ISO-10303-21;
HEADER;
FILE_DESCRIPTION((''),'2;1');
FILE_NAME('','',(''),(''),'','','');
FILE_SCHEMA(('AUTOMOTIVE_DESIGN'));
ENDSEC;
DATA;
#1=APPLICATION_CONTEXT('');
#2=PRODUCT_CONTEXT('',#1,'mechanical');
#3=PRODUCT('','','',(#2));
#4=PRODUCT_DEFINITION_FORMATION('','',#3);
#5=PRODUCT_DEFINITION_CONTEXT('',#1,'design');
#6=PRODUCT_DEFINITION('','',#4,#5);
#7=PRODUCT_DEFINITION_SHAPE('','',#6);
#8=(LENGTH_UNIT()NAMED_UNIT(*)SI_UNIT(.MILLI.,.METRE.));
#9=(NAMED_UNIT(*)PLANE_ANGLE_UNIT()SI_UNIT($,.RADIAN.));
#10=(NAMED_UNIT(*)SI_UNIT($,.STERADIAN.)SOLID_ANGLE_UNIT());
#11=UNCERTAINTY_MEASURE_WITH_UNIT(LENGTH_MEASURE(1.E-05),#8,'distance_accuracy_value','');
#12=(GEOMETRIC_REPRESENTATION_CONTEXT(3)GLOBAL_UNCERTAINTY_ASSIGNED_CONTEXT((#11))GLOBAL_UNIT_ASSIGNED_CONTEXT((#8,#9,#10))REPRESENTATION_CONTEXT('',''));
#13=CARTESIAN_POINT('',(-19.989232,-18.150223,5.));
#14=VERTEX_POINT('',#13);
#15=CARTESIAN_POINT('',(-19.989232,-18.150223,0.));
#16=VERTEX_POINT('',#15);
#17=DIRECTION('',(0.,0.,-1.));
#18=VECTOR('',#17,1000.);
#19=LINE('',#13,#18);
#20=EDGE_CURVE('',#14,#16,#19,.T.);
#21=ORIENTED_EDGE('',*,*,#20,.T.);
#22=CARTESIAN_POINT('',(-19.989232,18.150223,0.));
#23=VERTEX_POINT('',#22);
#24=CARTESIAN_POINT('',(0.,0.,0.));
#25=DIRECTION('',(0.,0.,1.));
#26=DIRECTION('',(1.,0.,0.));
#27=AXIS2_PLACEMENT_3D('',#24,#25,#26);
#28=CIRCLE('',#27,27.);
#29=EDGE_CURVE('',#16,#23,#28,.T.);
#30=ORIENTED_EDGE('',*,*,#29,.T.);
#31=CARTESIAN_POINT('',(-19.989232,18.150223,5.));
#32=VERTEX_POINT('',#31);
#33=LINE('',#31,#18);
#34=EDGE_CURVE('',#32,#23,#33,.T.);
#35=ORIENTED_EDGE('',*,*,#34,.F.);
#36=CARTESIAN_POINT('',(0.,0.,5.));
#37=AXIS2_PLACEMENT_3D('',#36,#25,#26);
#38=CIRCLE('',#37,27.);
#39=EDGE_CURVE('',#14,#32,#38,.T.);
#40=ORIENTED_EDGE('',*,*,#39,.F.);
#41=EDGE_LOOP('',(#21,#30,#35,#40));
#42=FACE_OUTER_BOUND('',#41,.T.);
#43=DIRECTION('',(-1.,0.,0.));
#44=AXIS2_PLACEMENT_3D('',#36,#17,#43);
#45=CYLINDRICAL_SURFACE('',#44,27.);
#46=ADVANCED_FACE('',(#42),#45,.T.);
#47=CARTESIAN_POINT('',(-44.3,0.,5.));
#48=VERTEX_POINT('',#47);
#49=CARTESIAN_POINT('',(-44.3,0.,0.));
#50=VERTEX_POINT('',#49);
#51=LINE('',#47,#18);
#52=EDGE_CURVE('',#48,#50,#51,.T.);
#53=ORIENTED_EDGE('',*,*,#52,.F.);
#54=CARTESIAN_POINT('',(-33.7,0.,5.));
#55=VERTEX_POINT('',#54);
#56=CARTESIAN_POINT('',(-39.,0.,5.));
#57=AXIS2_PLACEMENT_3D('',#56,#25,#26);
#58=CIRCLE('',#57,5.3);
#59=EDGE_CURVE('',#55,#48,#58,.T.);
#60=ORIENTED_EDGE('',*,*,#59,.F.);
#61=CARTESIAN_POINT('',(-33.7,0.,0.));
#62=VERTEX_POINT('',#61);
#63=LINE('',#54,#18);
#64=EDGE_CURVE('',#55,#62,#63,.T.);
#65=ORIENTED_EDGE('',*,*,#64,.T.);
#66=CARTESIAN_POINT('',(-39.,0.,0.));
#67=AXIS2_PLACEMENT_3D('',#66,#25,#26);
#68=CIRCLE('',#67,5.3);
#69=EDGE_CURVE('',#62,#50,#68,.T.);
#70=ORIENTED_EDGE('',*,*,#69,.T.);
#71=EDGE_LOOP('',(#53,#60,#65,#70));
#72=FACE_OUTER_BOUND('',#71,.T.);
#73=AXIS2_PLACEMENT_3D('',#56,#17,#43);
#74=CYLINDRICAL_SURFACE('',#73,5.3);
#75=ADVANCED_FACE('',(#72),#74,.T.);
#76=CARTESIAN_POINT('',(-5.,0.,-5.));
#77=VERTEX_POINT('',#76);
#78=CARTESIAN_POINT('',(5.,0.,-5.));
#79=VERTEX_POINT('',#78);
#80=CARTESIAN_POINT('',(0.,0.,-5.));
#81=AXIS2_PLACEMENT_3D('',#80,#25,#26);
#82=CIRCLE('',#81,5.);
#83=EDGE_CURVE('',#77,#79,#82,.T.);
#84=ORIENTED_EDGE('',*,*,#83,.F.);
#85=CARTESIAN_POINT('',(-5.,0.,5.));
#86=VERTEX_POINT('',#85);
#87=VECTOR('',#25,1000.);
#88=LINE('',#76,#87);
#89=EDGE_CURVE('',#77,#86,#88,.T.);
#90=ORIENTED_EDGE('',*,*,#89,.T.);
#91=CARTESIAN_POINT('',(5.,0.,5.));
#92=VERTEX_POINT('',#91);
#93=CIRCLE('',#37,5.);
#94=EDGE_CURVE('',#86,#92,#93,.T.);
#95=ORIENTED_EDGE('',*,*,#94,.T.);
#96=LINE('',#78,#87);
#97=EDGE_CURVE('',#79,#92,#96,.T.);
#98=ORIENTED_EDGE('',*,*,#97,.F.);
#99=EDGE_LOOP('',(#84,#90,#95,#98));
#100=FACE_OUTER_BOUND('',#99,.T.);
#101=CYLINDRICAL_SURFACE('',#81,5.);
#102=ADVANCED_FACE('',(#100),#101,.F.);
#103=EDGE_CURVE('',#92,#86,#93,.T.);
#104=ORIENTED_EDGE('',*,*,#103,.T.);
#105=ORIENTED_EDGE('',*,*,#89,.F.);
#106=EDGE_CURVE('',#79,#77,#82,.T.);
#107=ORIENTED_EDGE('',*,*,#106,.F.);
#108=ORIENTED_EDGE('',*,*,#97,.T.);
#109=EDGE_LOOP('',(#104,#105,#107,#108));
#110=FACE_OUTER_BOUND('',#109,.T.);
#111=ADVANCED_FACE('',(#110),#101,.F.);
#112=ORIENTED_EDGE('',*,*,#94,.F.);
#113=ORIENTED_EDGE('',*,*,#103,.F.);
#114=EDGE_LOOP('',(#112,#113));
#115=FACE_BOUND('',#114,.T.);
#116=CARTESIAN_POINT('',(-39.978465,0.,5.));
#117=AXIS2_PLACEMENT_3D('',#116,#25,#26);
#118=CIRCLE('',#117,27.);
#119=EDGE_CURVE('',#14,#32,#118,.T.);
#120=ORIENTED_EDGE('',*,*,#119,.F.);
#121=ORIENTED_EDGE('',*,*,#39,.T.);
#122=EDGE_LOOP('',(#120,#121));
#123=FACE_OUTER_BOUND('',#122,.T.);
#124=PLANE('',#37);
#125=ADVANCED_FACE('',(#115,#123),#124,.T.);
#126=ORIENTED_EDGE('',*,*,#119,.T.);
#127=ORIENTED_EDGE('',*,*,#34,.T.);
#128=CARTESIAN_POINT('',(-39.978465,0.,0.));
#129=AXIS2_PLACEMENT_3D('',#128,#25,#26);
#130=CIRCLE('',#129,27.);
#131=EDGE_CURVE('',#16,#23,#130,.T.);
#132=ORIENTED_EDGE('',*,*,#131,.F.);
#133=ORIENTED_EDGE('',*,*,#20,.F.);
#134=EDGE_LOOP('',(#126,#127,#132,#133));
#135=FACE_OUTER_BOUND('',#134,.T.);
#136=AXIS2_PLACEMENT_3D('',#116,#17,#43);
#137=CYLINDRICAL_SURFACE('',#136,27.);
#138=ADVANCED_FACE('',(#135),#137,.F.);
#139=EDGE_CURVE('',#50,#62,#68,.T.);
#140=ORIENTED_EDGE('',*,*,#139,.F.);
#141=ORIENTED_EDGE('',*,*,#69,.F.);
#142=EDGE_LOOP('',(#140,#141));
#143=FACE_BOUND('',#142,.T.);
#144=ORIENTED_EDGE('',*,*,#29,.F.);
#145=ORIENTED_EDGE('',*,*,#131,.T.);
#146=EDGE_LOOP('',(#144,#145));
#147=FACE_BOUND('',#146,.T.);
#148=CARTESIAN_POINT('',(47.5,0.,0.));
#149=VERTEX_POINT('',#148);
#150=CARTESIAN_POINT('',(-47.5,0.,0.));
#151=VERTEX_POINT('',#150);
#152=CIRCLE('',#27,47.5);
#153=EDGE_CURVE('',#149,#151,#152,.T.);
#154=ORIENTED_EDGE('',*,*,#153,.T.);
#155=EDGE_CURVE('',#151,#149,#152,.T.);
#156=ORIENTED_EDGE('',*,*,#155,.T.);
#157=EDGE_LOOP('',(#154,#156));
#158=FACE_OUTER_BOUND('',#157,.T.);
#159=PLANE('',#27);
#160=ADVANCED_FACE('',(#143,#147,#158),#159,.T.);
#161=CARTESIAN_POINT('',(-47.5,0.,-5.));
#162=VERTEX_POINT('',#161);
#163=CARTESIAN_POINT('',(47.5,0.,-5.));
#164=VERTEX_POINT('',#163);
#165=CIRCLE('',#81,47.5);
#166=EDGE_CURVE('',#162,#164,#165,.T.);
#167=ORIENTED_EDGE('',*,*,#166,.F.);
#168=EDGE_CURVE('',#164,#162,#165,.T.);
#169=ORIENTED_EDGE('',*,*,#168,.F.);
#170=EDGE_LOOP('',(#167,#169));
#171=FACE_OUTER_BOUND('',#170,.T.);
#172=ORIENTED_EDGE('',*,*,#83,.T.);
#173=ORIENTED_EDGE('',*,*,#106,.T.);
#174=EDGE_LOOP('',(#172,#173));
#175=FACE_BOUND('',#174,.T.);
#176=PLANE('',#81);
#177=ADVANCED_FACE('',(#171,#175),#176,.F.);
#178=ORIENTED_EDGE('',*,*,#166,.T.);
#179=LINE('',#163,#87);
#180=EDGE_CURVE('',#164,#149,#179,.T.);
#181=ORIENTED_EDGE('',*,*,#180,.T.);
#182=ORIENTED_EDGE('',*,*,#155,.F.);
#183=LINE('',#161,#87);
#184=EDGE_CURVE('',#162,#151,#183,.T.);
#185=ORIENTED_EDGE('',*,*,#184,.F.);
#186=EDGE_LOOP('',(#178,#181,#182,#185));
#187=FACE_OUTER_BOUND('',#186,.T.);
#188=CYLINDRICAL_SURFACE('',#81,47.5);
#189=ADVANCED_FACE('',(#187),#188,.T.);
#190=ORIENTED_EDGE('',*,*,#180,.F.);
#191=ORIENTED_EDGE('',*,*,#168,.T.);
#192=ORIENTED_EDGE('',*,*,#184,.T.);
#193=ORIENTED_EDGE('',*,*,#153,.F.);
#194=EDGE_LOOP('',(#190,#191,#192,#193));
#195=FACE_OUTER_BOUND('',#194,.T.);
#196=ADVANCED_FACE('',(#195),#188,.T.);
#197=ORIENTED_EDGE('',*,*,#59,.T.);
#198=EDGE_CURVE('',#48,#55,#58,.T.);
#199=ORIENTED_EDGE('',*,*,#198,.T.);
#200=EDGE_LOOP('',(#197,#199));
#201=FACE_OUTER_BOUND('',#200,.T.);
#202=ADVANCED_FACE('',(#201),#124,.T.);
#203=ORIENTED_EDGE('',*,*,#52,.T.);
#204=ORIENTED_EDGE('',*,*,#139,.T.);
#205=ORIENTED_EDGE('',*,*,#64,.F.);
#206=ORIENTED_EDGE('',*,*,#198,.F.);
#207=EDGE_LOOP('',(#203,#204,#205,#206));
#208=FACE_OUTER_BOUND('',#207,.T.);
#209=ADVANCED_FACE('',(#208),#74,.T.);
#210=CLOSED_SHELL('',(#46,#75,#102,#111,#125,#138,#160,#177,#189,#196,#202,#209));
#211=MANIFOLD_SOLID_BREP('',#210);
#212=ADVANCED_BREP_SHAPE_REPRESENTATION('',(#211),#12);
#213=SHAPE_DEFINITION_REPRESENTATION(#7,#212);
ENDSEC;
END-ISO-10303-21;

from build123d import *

# Parameters (mm, degrees)
DRIVE_WHEEL_PROFILE_R           = 47.5
DRIVE_WHEEL_PROFILE_R_2         = 5
DRIVE_DISC_95_DEPTH             = 5
LOCKING_START                   = 5
SKETCH1_3_R                     = 5
SKETCH1_3_R_2                   = 5.3
LOCKING_HUB_AND_DRIVE_PIN_DEPTH = 5


with BuildPart() as part:
    # Drive Wheel Profile → Drive Disc _95 (new body)
    with BuildSketch(Plane.XY):
        Circle(DRIVE_WHEEL_PROFILE_R)
        Circle(DRIVE_WHEEL_PROFILE_R_2, mode=Mode.SUBTRACT)
    extrude(amount=-DRIVE_DISC_95_DEPTH)

    # Sketch1_3 → Locking Hub and Drive Pin (add)
    # profile 1 of 2: a face of its own
    with BuildSketch(Plane.XY.offset(LOCKING_START)):
        with BuildLine():
            ThreePointArc((-19.989232296, -18.150222925), (-12.978464592, 0), (-19.989232296, 18.150222925))
            ThreePointArc((-19.989232296, 18.150222925), (27, 0), (-19.989232296, -18.150222925))
        make_face()
        Circle(SKETCH1_3_R, mode=Mode.SUBTRACT)
    # profile 2 of 2: a face of its own
    with BuildSketch(Plane.XY.offset(LOCKING_START)):
        with Locations((-39, 0)):
            Circle(SKETCH1_3_R_2)
    extrude(amount=-LOCKING_HUB_AND_DRIVE_PIN_DEPTH)


solid = part.part
